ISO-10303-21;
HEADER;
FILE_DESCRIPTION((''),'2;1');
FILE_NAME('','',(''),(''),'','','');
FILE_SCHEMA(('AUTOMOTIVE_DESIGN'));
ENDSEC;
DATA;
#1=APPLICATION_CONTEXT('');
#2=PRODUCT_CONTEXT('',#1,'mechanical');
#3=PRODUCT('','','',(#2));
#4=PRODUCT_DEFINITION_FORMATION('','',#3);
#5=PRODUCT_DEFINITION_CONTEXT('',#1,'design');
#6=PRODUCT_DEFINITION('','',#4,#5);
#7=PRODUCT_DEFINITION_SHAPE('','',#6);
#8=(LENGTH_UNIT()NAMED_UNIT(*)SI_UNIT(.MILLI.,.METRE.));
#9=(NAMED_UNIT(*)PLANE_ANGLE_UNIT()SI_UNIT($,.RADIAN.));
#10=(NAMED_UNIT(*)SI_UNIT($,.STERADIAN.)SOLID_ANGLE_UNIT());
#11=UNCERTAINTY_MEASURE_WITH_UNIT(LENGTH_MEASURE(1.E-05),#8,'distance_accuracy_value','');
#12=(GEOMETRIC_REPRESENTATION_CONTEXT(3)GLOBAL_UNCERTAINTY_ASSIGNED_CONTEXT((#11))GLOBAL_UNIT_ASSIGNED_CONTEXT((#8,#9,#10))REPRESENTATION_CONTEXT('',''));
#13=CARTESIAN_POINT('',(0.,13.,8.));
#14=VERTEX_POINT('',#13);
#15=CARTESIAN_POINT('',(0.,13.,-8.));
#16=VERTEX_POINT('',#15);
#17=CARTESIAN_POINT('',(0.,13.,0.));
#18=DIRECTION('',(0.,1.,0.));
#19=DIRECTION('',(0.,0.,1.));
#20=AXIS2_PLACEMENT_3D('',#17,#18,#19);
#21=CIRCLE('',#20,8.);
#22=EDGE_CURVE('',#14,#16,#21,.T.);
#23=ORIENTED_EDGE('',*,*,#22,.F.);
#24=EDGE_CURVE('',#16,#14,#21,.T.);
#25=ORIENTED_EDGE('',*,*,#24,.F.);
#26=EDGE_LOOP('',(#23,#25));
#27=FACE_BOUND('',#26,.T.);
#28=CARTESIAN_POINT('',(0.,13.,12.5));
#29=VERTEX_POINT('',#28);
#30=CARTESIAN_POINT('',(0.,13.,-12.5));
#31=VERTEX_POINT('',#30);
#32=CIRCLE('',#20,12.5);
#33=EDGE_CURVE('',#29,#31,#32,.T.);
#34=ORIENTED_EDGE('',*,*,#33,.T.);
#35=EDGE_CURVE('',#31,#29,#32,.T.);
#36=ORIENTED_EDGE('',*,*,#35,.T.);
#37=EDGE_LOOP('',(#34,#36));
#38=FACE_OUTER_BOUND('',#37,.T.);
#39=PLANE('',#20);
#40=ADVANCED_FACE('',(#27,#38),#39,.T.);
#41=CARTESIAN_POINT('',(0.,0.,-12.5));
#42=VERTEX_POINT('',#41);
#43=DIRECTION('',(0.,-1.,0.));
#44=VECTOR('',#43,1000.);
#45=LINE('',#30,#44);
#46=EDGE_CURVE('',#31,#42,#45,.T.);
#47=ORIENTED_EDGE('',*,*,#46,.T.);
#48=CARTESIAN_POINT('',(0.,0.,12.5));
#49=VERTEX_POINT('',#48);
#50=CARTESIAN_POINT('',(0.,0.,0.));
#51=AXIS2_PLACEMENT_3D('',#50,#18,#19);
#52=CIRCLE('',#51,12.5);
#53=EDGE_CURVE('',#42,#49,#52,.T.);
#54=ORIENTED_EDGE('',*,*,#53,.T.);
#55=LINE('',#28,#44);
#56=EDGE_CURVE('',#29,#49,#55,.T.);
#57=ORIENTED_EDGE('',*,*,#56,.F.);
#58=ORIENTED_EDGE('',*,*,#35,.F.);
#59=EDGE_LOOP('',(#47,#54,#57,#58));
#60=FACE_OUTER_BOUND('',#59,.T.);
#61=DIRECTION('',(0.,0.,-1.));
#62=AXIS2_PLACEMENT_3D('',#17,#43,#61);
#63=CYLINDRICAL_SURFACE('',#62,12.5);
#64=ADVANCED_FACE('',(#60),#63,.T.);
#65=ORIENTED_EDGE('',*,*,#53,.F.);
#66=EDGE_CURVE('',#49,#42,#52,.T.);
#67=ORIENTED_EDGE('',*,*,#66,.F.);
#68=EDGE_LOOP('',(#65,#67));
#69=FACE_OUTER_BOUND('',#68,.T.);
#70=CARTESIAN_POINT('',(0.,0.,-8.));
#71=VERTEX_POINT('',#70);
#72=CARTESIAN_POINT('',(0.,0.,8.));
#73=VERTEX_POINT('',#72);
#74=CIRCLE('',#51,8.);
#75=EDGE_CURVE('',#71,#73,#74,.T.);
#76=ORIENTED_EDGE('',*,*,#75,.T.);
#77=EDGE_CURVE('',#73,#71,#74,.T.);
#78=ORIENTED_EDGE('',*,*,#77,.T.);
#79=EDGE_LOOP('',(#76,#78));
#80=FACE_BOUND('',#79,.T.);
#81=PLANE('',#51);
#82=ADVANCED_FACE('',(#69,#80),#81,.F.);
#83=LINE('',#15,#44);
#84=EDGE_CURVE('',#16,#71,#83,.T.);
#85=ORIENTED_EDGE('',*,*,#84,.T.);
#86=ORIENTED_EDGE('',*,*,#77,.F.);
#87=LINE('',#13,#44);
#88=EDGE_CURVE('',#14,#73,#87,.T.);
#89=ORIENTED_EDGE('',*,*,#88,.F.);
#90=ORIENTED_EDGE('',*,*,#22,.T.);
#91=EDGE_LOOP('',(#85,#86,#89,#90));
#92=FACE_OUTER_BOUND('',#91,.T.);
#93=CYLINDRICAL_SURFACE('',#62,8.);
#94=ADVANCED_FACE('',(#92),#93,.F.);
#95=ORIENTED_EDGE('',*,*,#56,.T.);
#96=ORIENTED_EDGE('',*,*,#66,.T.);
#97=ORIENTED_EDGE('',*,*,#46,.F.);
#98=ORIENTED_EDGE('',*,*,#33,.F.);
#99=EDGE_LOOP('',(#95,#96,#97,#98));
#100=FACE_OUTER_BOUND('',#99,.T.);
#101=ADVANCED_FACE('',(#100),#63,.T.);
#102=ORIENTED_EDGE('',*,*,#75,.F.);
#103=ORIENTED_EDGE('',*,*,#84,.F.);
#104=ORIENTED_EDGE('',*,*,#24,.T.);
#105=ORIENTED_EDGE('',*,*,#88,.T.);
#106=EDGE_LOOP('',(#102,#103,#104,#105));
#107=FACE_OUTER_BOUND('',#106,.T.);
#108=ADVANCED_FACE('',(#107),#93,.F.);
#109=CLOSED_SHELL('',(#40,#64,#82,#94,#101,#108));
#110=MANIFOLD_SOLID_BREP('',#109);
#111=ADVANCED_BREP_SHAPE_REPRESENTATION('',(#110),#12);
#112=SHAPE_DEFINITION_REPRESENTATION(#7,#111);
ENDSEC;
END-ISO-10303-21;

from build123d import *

# Parameters (mm, degrees)
SKETCH_1_R      = 12.5
SKETCH_1_R_2    = 8
EXTRUDE_1_DEPTH = 13


with BuildPart() as part:
    # 草图1 → 凸台-拉伸1 (new body)
    with BuildSketch(Plane(origin=(0, 0, 0), x_dir=(1, 0, 0), z_dir=(0, 1, 0))):
        with Locations(Location((0, 0, 0), (0, 0, 90))):
            Circle(SKETCH_1_R)
        with Locations(Location((0, 0, 0), (0, 0, 90))):
            Circle(SKETCH_1_R_2, mode=Mode.SUBTRACT)
    extrude(amount=EXTRUDE_1_DEPTH)


solid = part.part
